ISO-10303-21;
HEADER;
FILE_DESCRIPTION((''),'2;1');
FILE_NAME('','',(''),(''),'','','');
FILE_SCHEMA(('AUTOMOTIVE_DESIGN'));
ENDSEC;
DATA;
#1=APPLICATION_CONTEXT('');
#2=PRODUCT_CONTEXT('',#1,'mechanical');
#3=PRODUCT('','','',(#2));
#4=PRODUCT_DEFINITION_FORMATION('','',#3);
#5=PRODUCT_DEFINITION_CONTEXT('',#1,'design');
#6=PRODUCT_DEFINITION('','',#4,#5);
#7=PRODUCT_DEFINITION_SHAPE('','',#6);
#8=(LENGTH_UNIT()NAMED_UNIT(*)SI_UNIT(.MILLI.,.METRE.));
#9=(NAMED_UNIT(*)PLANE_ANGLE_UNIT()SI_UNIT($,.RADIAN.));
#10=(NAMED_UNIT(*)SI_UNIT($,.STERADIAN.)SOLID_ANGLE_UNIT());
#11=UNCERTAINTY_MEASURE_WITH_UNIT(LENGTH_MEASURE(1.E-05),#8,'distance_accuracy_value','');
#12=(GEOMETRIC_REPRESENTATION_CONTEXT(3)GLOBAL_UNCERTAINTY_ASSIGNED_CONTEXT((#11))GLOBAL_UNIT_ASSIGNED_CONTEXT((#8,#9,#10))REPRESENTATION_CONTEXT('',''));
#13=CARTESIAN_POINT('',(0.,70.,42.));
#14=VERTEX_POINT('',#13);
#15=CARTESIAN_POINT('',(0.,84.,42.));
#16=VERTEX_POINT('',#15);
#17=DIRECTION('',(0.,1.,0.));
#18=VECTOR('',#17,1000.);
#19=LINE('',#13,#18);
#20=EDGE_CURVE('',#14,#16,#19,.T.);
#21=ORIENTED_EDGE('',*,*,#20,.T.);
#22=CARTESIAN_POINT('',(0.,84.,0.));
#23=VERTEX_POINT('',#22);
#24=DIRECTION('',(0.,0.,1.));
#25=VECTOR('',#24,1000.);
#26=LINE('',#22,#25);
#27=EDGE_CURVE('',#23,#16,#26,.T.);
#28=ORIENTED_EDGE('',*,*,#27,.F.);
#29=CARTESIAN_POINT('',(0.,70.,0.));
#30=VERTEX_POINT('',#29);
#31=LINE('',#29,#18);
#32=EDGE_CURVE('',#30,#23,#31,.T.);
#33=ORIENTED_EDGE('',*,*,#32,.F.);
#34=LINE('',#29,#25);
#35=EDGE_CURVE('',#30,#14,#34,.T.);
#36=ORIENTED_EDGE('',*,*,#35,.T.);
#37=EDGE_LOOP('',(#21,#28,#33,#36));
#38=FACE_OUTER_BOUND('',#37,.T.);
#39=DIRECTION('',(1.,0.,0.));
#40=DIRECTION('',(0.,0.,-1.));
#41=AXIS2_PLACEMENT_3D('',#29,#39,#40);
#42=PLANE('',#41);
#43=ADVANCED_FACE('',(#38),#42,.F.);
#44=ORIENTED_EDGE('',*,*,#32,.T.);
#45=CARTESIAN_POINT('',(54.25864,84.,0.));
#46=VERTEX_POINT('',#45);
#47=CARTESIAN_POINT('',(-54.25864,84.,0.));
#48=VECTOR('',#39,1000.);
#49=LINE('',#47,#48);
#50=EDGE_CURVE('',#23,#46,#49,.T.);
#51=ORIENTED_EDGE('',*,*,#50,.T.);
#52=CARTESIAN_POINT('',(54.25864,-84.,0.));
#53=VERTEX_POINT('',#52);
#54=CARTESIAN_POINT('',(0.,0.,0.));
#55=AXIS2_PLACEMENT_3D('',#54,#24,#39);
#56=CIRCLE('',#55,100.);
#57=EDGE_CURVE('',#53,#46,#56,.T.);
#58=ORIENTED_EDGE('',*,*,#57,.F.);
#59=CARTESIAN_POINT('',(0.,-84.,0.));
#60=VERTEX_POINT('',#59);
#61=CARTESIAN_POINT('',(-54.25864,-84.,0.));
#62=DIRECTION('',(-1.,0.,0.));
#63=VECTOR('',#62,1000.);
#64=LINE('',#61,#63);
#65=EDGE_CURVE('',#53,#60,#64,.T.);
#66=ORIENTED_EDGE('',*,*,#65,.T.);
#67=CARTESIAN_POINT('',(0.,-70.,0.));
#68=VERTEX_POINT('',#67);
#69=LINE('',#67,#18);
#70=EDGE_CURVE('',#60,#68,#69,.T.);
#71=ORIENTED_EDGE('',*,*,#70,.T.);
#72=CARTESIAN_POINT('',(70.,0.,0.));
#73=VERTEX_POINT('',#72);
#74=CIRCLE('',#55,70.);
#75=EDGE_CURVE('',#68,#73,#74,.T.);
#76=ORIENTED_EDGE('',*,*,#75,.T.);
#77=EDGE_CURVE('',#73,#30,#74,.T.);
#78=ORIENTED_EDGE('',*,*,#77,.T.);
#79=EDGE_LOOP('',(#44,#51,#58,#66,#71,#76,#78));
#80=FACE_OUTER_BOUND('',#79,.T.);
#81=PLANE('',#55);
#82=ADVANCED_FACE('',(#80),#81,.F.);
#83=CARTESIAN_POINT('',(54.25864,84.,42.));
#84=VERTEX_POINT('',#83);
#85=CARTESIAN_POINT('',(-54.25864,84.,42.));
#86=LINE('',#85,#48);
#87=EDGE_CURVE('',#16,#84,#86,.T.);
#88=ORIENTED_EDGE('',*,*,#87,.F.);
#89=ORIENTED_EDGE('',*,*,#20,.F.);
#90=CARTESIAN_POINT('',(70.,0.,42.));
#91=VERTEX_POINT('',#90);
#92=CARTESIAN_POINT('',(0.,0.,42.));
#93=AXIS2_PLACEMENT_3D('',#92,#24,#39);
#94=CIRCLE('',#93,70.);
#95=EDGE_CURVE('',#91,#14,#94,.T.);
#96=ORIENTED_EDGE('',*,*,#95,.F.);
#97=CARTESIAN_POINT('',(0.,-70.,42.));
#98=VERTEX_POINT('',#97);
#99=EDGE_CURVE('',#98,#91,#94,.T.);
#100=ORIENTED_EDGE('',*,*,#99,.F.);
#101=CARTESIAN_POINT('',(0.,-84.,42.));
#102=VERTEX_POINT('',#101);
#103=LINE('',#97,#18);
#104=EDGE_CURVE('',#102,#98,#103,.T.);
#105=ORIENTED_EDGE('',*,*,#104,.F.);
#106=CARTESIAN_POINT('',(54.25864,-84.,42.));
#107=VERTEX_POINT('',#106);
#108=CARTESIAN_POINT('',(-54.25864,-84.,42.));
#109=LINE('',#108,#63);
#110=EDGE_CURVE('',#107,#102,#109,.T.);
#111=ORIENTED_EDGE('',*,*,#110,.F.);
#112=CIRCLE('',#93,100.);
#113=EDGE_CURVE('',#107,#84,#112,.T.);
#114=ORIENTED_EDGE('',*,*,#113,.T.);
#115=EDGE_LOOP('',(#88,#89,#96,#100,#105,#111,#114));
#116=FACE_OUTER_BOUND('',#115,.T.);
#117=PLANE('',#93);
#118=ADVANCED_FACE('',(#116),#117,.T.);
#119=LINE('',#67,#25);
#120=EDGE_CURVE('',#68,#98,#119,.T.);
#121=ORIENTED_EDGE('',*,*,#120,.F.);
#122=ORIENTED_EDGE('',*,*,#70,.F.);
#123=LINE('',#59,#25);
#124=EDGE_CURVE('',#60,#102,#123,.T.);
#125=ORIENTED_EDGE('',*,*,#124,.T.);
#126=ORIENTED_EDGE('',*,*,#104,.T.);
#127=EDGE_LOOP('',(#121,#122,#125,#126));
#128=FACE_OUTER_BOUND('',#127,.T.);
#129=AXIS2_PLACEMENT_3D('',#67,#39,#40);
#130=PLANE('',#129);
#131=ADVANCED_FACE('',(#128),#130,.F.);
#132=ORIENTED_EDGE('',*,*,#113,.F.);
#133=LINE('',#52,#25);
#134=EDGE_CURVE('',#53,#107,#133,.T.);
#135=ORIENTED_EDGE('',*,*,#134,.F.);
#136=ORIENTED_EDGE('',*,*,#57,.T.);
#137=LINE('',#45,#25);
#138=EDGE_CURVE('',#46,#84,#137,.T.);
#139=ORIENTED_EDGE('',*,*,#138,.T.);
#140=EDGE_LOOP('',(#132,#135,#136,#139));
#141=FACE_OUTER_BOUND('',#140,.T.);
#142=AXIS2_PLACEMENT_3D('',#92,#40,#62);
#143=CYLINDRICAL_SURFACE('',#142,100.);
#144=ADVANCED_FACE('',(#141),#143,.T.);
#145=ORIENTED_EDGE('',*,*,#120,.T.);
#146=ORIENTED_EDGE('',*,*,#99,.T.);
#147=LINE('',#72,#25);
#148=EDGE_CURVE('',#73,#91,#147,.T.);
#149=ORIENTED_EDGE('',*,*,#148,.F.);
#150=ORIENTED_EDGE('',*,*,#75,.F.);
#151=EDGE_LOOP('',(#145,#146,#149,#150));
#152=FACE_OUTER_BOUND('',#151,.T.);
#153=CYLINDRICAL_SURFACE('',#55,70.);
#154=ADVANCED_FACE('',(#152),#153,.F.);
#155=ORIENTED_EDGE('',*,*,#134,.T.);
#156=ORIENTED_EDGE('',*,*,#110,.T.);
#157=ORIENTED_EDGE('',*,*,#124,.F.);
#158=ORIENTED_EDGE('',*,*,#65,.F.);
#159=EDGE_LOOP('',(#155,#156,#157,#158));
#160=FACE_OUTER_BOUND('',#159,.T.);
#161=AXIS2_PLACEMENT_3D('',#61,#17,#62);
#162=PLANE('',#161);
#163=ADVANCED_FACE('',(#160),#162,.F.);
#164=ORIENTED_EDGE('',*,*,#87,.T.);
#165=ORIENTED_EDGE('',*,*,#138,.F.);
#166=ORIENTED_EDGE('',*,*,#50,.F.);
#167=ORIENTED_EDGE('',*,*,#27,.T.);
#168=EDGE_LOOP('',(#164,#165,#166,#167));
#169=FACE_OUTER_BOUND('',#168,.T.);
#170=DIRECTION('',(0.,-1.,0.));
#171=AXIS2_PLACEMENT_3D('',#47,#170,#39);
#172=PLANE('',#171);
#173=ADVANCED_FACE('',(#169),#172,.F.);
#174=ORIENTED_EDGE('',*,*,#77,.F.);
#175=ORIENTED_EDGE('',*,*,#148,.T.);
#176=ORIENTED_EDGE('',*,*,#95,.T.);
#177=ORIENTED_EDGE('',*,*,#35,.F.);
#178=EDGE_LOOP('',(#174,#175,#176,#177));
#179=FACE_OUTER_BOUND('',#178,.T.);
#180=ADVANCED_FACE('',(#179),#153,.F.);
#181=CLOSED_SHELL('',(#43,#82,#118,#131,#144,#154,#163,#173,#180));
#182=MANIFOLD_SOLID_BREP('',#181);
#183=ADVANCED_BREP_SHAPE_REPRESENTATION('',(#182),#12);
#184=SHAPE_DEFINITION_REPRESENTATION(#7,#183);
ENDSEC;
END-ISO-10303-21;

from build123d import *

# Parameters (mm, degrees)
SKETCH_1_R          = 100
EXTRUDE_1_DEPTH     = 42
CUT_EXTRUDE_1_DEPTH = 148.526268847
CUT_EXTRUDE_2_DEPTH = 138.186005117


with BuildPart() as part:
    # 草图1 → 凸台-拉伸1 (new body)
    with BuildSketch(Plane.XY):
        with Locations(Location((0, 0, 0), (0, 0, 180))):
            Circle(SKETCH_1_R)
    extrude(amount=EXTRUDE_1_DEPTH)

    # 草图2 → 切除-拉伸1 (cut, through all)
    with BuildSketch(Plane.XY.offset(42)):
        with BuildLine():
            Line((-54.258639865, 84), (54.258639865, 84))
            ThreePointArc((54.258639865, 84), (0, 100), (-54.258639865, 84))
        make_face()
        with BuildLine():
            Line((-54.258639865, -84), (54.258639865, -84))
            ThreePointArc((54.258639865, -84), (0, -100), (-54.258639865, -84))
        make_face()
    extrude(amount=-CUT_EXTRUDE_1_DEPTH, mode=Mode.SUBTRACT)

    # 草图3 → 切除-拉伸2 (cut, through all)
    with BuildSketch(Plane.XY.offset(42)):
        with BuildLine():
            Line((0, 70), (0, 84))
            Line((0, 84), (-54.258639865, 84))
            ThreePointArc((-54.258639865, 84), (-100, 0), (-54.258639865, -84))
            Line((-54.258639865, -84), (0, -84))
            Line((0, -84), (0, -70))
            ThreePointArc((0, -70), (70, 0), (0, 70))
        make_face()
    extrude(amount=-CUT_EXTRUDE_2_DEPTH, mode=Mode.SUBTRACT)


solid = part.part
